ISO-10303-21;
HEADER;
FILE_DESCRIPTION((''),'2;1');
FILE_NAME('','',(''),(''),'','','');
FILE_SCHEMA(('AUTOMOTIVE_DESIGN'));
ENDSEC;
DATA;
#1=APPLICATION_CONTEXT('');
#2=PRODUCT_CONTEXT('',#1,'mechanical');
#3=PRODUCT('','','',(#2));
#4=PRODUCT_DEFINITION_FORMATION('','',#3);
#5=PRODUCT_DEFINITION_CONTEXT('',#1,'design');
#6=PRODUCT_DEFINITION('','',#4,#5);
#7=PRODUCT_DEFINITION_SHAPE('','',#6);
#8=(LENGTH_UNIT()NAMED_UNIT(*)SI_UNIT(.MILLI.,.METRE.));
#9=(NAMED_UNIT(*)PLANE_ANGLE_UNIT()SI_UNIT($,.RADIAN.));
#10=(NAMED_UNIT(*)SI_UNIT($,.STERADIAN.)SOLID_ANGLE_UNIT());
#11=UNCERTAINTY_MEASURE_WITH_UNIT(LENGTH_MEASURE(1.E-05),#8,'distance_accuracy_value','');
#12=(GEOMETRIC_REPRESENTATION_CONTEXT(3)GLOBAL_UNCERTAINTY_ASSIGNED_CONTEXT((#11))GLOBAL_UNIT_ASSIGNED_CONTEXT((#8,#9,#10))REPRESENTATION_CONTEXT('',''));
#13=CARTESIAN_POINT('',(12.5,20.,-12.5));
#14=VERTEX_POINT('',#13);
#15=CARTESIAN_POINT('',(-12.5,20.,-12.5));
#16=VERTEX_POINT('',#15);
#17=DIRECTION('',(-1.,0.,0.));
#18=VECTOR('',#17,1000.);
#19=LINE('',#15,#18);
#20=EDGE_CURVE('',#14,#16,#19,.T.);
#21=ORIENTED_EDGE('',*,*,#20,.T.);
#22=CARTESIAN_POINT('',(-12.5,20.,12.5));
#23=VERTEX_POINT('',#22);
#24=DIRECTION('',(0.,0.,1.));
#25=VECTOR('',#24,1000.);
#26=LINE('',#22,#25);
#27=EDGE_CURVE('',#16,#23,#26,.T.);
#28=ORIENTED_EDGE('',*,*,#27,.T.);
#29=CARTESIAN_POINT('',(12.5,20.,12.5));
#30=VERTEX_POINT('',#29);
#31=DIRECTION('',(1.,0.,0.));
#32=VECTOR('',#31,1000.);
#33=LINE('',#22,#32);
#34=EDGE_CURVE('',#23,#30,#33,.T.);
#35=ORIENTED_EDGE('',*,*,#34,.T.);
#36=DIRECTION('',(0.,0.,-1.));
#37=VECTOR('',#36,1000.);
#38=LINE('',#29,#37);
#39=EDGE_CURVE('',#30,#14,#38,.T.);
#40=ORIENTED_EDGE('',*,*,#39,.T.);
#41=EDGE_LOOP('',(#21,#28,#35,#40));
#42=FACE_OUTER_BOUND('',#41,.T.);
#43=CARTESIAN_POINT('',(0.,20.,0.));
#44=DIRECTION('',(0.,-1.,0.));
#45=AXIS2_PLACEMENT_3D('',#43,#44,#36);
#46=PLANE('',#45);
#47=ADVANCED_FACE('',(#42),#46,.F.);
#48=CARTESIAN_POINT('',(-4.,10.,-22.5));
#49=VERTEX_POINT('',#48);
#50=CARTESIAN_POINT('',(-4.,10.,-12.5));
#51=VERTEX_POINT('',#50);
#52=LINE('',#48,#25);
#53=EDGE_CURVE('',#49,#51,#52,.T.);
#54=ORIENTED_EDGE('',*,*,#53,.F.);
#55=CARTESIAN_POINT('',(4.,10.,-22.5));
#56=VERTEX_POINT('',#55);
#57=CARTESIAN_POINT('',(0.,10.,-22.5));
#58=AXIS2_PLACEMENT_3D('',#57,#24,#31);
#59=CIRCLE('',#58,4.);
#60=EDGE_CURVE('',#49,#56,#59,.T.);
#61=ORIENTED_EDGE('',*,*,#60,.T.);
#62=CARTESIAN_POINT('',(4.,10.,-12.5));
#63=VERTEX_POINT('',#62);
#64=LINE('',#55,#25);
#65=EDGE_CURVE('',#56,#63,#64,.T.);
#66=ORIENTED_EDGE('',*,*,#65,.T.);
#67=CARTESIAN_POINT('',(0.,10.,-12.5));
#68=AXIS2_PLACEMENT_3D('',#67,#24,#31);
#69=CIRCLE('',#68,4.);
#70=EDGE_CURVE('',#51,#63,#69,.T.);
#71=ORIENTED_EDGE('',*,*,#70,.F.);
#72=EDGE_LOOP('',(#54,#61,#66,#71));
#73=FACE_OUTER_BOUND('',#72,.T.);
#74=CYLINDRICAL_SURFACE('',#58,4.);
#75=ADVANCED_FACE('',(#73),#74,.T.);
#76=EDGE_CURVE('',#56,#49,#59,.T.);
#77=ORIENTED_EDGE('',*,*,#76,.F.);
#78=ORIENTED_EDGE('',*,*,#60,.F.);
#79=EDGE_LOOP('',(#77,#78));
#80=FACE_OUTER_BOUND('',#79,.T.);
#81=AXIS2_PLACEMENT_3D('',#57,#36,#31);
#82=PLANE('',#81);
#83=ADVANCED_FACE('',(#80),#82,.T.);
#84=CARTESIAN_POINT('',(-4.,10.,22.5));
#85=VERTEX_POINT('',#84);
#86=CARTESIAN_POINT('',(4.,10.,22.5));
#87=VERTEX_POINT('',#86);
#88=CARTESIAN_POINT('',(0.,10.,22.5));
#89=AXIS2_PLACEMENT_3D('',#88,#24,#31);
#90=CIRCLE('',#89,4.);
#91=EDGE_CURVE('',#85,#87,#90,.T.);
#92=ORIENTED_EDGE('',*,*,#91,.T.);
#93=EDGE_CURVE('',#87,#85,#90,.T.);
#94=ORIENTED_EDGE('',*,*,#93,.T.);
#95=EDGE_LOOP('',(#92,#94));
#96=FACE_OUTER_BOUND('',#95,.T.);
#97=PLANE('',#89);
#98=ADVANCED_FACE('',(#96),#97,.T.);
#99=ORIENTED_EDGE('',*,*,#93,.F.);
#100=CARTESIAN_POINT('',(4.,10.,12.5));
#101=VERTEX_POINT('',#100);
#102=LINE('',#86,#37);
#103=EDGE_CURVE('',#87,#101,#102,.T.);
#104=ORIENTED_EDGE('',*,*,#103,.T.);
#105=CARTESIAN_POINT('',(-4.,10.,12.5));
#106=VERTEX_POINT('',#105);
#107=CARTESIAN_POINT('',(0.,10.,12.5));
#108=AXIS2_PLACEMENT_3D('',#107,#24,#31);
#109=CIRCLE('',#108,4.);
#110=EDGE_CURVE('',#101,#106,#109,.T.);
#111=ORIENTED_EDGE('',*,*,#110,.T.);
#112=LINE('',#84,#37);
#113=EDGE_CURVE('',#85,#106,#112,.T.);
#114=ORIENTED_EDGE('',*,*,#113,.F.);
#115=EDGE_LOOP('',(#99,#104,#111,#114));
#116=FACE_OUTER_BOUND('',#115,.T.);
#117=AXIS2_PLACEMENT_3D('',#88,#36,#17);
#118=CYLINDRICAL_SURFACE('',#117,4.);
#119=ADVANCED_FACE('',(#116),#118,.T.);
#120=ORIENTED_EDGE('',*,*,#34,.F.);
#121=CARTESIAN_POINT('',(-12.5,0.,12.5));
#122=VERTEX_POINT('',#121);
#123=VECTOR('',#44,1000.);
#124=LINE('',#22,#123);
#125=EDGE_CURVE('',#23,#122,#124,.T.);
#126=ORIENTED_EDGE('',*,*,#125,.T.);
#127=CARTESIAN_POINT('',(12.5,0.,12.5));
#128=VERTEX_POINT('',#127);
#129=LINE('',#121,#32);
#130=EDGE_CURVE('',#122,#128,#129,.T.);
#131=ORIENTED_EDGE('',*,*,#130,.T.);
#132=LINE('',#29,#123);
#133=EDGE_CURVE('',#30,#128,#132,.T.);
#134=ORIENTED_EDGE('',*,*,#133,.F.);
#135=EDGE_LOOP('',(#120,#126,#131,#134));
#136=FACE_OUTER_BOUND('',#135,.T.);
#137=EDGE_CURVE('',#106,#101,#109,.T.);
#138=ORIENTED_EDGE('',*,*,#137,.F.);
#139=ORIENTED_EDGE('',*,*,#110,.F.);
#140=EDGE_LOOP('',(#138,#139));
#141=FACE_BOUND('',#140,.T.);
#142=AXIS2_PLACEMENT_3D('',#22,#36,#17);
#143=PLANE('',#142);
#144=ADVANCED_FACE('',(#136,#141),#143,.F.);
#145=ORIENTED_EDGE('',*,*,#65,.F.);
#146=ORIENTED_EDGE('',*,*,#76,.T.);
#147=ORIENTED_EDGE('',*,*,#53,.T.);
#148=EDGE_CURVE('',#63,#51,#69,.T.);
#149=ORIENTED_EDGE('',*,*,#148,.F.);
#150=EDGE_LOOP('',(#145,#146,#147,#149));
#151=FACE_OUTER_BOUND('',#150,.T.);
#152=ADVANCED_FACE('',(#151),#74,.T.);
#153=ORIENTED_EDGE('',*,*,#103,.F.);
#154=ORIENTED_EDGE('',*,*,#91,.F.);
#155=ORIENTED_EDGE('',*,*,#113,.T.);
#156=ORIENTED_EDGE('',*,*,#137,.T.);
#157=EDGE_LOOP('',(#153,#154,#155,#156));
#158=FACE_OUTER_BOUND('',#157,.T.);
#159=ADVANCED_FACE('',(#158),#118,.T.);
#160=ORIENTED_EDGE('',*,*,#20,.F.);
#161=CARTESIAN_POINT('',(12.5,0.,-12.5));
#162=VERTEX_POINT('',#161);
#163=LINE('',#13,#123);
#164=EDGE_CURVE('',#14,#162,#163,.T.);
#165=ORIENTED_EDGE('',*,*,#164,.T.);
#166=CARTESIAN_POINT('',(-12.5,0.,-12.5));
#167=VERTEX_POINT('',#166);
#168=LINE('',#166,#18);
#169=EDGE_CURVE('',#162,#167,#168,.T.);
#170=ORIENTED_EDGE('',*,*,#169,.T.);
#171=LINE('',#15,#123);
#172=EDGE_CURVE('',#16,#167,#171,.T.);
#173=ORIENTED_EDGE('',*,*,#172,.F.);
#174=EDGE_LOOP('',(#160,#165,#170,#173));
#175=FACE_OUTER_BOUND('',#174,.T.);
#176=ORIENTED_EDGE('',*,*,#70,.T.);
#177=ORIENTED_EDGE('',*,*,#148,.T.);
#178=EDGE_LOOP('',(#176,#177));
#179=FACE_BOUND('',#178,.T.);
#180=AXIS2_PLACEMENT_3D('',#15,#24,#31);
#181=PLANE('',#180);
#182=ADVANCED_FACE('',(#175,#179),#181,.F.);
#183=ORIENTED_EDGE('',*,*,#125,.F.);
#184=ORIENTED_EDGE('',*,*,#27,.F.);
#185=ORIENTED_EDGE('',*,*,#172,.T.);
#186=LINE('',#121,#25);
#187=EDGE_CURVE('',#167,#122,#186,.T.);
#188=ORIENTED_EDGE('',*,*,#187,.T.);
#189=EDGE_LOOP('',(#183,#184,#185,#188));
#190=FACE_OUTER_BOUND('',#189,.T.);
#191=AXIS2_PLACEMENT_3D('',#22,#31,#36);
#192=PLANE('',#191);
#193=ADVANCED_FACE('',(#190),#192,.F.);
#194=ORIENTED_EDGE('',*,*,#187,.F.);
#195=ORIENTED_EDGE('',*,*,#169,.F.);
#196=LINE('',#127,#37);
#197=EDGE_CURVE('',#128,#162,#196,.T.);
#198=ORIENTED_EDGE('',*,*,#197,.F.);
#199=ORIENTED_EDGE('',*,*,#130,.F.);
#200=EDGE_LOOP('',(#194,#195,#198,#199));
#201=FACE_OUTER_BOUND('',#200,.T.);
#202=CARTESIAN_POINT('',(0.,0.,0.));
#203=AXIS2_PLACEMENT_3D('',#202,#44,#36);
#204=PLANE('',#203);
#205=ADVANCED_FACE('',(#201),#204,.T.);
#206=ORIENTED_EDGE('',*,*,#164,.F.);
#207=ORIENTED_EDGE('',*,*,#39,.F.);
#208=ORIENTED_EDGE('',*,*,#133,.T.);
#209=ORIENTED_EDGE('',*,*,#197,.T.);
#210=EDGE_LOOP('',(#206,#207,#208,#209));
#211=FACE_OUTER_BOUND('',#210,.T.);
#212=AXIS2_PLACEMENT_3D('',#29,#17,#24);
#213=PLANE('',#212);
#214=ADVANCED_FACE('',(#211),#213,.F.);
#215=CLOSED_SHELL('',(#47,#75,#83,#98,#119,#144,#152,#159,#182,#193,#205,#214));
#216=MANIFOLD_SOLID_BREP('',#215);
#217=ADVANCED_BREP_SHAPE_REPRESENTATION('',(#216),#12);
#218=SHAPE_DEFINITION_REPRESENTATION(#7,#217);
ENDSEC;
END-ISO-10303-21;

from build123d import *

# Parameters (mm, degrees)
SKETCH1_W           = 25
SKETCH1_H           = 25
BOSS_EXTRUDE1_DEPTH = 20
SKETCH2_R           = 4
BOSS_EXTRUDE2_DEPTH = 10


with BuildPart() as part:
    # Sketch1 → Boss-Extrude1 (new body)
    with BuildSketch(Plane(origin=(0, 0, 0), x_dir=(1, 0, 0), z_dir=(0, 1, 0))):
        Rectangle(SKETCH1_W, SKETCH1_H)
    extrude(amount=BOSS_EXTRUDE1_DEPTH)

    # Sketch2 → Boss-Extrude2 (add)
    with BuildSketch(Plane.XY.offset(12.5)):
        with Locations((0, 10)):
            Circle(SKETCH2_R)
    boss_extrude2 = extrude(amount=BOSS_EXTRUDE2_DEPTH)

    # Mirror1: Boss-Extrude2 across plane
    add(boss_extrude2.mirror(Plane.XY))


solid = part.part
